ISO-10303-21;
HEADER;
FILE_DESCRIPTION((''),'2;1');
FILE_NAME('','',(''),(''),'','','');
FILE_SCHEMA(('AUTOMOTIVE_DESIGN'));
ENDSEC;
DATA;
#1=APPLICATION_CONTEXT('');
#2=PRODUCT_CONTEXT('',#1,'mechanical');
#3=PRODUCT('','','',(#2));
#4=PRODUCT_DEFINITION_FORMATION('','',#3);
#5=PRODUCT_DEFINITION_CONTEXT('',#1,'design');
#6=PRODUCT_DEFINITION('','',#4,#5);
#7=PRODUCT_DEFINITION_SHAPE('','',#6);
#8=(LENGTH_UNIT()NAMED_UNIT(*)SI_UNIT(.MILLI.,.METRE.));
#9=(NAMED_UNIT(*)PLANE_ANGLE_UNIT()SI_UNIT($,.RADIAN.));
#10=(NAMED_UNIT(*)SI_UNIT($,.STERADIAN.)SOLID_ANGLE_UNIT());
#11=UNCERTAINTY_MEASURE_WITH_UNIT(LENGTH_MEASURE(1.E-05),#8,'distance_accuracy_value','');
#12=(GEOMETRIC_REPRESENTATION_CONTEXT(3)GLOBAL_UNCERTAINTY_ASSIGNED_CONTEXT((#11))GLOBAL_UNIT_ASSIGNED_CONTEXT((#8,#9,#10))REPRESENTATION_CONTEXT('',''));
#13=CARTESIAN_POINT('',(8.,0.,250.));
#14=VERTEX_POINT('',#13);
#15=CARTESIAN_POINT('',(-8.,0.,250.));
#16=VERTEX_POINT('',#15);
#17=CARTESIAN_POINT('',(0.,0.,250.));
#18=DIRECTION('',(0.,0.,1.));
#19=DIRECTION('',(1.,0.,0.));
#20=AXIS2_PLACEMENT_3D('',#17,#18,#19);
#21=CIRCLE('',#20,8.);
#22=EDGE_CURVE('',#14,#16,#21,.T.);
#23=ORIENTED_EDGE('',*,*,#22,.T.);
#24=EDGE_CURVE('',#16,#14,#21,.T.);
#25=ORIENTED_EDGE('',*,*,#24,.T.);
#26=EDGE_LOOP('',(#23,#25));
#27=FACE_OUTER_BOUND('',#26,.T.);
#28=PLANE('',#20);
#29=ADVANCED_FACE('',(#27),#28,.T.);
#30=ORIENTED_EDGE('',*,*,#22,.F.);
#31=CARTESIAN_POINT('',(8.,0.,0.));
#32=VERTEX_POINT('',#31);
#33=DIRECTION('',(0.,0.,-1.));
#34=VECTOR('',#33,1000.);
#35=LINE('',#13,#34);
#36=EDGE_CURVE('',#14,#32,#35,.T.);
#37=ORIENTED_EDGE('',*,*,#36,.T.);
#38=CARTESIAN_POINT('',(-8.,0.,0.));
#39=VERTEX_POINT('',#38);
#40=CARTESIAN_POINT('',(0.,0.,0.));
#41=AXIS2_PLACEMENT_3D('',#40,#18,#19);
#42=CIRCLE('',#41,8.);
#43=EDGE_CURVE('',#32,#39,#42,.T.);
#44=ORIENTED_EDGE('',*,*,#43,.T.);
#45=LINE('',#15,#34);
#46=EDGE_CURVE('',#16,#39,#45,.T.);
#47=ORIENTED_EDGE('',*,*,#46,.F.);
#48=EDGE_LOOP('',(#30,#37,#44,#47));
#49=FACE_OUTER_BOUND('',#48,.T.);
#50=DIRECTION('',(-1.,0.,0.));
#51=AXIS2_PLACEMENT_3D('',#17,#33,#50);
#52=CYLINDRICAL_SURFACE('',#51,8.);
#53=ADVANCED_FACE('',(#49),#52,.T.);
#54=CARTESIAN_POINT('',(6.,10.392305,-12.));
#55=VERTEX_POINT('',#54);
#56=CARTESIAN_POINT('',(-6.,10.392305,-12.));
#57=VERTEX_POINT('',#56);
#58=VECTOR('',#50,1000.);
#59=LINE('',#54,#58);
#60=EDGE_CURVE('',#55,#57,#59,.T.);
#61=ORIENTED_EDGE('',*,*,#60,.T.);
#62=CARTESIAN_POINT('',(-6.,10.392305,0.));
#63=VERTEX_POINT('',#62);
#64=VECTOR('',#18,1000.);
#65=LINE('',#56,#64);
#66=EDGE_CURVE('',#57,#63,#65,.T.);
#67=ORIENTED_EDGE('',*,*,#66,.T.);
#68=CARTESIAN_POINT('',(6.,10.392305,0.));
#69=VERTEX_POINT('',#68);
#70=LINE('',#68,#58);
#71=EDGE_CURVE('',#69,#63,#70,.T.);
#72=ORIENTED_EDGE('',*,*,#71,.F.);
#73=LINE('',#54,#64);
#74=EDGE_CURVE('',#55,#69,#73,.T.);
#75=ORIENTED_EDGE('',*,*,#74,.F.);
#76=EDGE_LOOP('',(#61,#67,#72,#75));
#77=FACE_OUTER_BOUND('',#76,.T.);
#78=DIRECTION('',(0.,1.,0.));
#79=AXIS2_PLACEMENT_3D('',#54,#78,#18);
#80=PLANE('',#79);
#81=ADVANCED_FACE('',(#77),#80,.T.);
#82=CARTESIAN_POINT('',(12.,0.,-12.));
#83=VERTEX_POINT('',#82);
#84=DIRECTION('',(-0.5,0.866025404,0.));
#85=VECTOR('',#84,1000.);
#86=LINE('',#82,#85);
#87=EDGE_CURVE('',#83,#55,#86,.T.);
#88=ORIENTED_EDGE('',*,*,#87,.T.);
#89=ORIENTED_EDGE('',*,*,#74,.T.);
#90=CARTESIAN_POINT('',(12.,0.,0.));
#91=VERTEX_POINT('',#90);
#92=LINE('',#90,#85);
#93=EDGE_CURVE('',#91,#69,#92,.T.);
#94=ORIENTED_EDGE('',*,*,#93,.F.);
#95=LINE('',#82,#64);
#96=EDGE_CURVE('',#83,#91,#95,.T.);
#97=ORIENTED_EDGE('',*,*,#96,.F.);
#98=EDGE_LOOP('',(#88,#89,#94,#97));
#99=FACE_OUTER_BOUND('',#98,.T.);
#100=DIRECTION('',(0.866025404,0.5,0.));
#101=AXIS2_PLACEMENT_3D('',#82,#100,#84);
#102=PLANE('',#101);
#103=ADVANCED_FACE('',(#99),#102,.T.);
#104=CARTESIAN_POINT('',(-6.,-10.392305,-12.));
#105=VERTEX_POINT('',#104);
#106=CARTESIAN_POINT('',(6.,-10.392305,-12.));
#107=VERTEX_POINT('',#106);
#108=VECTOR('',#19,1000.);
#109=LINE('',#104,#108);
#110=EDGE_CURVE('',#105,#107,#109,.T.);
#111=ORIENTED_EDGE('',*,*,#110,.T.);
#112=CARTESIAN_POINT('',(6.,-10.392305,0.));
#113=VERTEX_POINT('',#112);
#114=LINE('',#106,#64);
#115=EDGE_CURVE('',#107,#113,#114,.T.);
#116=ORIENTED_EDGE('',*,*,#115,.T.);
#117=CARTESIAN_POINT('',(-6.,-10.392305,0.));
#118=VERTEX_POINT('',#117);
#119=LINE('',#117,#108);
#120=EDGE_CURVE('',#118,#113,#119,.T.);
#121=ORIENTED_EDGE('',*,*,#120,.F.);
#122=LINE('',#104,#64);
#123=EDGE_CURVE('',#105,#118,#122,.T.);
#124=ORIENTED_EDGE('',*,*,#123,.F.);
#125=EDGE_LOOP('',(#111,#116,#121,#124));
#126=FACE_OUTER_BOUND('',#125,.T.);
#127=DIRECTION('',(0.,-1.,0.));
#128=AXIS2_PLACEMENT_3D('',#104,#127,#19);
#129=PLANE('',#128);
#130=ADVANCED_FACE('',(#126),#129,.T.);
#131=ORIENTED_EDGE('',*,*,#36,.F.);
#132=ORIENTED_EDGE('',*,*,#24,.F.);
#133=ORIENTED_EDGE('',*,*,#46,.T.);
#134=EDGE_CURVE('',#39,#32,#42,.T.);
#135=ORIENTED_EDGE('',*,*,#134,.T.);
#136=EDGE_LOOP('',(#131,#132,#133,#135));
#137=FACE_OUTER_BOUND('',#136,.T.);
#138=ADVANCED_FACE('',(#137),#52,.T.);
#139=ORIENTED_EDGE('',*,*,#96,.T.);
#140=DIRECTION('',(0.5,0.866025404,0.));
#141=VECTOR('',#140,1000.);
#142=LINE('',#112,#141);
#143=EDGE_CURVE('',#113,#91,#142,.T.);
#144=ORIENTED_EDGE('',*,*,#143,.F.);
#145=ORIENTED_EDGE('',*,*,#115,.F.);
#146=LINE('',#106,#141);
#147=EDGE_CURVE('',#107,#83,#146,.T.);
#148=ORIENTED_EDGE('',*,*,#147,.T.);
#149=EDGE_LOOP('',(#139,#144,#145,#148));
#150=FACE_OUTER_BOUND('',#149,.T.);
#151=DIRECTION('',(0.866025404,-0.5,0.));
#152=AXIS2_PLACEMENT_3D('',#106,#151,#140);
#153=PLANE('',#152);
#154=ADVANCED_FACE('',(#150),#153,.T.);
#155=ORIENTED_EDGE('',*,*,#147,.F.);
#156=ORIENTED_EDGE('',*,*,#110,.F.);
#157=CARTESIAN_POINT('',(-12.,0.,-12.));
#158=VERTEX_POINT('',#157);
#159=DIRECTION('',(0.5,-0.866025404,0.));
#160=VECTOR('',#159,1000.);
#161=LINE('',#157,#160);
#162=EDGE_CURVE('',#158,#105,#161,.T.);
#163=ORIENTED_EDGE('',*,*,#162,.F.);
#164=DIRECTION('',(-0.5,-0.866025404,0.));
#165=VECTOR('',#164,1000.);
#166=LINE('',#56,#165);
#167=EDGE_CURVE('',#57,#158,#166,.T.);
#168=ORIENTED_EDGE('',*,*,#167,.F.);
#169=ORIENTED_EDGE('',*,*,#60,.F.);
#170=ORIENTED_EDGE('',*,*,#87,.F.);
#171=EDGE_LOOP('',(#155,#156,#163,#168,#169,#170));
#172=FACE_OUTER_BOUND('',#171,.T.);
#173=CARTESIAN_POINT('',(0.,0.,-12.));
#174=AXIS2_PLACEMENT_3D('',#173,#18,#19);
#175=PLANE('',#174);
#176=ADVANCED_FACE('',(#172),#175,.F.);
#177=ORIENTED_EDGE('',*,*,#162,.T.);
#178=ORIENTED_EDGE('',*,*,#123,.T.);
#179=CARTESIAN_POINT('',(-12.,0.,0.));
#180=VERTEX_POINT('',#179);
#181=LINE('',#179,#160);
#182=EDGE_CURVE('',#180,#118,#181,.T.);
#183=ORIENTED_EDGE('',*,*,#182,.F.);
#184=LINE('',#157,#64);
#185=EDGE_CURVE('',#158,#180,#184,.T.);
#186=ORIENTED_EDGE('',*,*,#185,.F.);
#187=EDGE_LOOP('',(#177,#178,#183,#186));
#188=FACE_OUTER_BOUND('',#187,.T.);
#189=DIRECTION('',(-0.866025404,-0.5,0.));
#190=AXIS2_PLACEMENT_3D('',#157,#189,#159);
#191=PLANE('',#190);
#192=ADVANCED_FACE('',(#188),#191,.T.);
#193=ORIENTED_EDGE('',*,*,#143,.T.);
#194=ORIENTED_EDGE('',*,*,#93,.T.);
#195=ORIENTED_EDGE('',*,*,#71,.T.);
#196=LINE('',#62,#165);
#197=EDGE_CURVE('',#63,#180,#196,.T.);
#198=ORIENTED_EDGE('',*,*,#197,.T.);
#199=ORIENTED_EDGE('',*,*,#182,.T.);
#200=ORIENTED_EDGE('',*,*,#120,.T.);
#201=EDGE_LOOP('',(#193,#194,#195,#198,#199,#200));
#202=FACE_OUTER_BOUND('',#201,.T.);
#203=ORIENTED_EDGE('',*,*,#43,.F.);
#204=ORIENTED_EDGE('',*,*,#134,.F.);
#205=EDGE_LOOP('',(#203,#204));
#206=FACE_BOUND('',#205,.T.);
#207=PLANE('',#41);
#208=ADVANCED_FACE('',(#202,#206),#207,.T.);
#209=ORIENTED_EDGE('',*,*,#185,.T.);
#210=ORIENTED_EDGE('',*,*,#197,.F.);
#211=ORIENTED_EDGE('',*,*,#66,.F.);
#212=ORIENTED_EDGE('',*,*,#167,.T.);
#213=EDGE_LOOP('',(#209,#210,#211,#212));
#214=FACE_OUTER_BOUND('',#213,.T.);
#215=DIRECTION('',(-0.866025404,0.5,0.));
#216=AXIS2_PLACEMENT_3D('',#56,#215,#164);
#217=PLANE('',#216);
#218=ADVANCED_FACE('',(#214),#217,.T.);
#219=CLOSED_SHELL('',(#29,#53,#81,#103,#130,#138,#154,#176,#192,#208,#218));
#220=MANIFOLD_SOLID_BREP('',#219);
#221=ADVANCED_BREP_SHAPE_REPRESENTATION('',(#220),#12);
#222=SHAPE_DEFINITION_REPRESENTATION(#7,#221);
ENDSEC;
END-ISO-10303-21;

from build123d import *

# Parameters (mm, degrees)
SKETCH_1_R      = 8
EXTRUDE_1_DEPTH = 250
EXTRUDE_2_DEPTH = 12


with BuildPart() as part:
    # 草图1 → 凸台-拉伸1 (new body)
    with BuildSketch(Plane.XY):
        Circle(SKETCH_1_R)
    extrude(amount=EXTRUDE_1_DEPTH)

    # 草图2 → 凸台-拉伸2 (add)
    with BuildSketch(Plane.XY):
        Polygon((12, 0), (6, 10.392304845), (-6, 10.392304845), (-12, 0), (-6, -10.392304845), (6, -10.392304845), align=None)
    extrude(amount=-EXTRUDE_2_DEPTH)


solid = part.part
